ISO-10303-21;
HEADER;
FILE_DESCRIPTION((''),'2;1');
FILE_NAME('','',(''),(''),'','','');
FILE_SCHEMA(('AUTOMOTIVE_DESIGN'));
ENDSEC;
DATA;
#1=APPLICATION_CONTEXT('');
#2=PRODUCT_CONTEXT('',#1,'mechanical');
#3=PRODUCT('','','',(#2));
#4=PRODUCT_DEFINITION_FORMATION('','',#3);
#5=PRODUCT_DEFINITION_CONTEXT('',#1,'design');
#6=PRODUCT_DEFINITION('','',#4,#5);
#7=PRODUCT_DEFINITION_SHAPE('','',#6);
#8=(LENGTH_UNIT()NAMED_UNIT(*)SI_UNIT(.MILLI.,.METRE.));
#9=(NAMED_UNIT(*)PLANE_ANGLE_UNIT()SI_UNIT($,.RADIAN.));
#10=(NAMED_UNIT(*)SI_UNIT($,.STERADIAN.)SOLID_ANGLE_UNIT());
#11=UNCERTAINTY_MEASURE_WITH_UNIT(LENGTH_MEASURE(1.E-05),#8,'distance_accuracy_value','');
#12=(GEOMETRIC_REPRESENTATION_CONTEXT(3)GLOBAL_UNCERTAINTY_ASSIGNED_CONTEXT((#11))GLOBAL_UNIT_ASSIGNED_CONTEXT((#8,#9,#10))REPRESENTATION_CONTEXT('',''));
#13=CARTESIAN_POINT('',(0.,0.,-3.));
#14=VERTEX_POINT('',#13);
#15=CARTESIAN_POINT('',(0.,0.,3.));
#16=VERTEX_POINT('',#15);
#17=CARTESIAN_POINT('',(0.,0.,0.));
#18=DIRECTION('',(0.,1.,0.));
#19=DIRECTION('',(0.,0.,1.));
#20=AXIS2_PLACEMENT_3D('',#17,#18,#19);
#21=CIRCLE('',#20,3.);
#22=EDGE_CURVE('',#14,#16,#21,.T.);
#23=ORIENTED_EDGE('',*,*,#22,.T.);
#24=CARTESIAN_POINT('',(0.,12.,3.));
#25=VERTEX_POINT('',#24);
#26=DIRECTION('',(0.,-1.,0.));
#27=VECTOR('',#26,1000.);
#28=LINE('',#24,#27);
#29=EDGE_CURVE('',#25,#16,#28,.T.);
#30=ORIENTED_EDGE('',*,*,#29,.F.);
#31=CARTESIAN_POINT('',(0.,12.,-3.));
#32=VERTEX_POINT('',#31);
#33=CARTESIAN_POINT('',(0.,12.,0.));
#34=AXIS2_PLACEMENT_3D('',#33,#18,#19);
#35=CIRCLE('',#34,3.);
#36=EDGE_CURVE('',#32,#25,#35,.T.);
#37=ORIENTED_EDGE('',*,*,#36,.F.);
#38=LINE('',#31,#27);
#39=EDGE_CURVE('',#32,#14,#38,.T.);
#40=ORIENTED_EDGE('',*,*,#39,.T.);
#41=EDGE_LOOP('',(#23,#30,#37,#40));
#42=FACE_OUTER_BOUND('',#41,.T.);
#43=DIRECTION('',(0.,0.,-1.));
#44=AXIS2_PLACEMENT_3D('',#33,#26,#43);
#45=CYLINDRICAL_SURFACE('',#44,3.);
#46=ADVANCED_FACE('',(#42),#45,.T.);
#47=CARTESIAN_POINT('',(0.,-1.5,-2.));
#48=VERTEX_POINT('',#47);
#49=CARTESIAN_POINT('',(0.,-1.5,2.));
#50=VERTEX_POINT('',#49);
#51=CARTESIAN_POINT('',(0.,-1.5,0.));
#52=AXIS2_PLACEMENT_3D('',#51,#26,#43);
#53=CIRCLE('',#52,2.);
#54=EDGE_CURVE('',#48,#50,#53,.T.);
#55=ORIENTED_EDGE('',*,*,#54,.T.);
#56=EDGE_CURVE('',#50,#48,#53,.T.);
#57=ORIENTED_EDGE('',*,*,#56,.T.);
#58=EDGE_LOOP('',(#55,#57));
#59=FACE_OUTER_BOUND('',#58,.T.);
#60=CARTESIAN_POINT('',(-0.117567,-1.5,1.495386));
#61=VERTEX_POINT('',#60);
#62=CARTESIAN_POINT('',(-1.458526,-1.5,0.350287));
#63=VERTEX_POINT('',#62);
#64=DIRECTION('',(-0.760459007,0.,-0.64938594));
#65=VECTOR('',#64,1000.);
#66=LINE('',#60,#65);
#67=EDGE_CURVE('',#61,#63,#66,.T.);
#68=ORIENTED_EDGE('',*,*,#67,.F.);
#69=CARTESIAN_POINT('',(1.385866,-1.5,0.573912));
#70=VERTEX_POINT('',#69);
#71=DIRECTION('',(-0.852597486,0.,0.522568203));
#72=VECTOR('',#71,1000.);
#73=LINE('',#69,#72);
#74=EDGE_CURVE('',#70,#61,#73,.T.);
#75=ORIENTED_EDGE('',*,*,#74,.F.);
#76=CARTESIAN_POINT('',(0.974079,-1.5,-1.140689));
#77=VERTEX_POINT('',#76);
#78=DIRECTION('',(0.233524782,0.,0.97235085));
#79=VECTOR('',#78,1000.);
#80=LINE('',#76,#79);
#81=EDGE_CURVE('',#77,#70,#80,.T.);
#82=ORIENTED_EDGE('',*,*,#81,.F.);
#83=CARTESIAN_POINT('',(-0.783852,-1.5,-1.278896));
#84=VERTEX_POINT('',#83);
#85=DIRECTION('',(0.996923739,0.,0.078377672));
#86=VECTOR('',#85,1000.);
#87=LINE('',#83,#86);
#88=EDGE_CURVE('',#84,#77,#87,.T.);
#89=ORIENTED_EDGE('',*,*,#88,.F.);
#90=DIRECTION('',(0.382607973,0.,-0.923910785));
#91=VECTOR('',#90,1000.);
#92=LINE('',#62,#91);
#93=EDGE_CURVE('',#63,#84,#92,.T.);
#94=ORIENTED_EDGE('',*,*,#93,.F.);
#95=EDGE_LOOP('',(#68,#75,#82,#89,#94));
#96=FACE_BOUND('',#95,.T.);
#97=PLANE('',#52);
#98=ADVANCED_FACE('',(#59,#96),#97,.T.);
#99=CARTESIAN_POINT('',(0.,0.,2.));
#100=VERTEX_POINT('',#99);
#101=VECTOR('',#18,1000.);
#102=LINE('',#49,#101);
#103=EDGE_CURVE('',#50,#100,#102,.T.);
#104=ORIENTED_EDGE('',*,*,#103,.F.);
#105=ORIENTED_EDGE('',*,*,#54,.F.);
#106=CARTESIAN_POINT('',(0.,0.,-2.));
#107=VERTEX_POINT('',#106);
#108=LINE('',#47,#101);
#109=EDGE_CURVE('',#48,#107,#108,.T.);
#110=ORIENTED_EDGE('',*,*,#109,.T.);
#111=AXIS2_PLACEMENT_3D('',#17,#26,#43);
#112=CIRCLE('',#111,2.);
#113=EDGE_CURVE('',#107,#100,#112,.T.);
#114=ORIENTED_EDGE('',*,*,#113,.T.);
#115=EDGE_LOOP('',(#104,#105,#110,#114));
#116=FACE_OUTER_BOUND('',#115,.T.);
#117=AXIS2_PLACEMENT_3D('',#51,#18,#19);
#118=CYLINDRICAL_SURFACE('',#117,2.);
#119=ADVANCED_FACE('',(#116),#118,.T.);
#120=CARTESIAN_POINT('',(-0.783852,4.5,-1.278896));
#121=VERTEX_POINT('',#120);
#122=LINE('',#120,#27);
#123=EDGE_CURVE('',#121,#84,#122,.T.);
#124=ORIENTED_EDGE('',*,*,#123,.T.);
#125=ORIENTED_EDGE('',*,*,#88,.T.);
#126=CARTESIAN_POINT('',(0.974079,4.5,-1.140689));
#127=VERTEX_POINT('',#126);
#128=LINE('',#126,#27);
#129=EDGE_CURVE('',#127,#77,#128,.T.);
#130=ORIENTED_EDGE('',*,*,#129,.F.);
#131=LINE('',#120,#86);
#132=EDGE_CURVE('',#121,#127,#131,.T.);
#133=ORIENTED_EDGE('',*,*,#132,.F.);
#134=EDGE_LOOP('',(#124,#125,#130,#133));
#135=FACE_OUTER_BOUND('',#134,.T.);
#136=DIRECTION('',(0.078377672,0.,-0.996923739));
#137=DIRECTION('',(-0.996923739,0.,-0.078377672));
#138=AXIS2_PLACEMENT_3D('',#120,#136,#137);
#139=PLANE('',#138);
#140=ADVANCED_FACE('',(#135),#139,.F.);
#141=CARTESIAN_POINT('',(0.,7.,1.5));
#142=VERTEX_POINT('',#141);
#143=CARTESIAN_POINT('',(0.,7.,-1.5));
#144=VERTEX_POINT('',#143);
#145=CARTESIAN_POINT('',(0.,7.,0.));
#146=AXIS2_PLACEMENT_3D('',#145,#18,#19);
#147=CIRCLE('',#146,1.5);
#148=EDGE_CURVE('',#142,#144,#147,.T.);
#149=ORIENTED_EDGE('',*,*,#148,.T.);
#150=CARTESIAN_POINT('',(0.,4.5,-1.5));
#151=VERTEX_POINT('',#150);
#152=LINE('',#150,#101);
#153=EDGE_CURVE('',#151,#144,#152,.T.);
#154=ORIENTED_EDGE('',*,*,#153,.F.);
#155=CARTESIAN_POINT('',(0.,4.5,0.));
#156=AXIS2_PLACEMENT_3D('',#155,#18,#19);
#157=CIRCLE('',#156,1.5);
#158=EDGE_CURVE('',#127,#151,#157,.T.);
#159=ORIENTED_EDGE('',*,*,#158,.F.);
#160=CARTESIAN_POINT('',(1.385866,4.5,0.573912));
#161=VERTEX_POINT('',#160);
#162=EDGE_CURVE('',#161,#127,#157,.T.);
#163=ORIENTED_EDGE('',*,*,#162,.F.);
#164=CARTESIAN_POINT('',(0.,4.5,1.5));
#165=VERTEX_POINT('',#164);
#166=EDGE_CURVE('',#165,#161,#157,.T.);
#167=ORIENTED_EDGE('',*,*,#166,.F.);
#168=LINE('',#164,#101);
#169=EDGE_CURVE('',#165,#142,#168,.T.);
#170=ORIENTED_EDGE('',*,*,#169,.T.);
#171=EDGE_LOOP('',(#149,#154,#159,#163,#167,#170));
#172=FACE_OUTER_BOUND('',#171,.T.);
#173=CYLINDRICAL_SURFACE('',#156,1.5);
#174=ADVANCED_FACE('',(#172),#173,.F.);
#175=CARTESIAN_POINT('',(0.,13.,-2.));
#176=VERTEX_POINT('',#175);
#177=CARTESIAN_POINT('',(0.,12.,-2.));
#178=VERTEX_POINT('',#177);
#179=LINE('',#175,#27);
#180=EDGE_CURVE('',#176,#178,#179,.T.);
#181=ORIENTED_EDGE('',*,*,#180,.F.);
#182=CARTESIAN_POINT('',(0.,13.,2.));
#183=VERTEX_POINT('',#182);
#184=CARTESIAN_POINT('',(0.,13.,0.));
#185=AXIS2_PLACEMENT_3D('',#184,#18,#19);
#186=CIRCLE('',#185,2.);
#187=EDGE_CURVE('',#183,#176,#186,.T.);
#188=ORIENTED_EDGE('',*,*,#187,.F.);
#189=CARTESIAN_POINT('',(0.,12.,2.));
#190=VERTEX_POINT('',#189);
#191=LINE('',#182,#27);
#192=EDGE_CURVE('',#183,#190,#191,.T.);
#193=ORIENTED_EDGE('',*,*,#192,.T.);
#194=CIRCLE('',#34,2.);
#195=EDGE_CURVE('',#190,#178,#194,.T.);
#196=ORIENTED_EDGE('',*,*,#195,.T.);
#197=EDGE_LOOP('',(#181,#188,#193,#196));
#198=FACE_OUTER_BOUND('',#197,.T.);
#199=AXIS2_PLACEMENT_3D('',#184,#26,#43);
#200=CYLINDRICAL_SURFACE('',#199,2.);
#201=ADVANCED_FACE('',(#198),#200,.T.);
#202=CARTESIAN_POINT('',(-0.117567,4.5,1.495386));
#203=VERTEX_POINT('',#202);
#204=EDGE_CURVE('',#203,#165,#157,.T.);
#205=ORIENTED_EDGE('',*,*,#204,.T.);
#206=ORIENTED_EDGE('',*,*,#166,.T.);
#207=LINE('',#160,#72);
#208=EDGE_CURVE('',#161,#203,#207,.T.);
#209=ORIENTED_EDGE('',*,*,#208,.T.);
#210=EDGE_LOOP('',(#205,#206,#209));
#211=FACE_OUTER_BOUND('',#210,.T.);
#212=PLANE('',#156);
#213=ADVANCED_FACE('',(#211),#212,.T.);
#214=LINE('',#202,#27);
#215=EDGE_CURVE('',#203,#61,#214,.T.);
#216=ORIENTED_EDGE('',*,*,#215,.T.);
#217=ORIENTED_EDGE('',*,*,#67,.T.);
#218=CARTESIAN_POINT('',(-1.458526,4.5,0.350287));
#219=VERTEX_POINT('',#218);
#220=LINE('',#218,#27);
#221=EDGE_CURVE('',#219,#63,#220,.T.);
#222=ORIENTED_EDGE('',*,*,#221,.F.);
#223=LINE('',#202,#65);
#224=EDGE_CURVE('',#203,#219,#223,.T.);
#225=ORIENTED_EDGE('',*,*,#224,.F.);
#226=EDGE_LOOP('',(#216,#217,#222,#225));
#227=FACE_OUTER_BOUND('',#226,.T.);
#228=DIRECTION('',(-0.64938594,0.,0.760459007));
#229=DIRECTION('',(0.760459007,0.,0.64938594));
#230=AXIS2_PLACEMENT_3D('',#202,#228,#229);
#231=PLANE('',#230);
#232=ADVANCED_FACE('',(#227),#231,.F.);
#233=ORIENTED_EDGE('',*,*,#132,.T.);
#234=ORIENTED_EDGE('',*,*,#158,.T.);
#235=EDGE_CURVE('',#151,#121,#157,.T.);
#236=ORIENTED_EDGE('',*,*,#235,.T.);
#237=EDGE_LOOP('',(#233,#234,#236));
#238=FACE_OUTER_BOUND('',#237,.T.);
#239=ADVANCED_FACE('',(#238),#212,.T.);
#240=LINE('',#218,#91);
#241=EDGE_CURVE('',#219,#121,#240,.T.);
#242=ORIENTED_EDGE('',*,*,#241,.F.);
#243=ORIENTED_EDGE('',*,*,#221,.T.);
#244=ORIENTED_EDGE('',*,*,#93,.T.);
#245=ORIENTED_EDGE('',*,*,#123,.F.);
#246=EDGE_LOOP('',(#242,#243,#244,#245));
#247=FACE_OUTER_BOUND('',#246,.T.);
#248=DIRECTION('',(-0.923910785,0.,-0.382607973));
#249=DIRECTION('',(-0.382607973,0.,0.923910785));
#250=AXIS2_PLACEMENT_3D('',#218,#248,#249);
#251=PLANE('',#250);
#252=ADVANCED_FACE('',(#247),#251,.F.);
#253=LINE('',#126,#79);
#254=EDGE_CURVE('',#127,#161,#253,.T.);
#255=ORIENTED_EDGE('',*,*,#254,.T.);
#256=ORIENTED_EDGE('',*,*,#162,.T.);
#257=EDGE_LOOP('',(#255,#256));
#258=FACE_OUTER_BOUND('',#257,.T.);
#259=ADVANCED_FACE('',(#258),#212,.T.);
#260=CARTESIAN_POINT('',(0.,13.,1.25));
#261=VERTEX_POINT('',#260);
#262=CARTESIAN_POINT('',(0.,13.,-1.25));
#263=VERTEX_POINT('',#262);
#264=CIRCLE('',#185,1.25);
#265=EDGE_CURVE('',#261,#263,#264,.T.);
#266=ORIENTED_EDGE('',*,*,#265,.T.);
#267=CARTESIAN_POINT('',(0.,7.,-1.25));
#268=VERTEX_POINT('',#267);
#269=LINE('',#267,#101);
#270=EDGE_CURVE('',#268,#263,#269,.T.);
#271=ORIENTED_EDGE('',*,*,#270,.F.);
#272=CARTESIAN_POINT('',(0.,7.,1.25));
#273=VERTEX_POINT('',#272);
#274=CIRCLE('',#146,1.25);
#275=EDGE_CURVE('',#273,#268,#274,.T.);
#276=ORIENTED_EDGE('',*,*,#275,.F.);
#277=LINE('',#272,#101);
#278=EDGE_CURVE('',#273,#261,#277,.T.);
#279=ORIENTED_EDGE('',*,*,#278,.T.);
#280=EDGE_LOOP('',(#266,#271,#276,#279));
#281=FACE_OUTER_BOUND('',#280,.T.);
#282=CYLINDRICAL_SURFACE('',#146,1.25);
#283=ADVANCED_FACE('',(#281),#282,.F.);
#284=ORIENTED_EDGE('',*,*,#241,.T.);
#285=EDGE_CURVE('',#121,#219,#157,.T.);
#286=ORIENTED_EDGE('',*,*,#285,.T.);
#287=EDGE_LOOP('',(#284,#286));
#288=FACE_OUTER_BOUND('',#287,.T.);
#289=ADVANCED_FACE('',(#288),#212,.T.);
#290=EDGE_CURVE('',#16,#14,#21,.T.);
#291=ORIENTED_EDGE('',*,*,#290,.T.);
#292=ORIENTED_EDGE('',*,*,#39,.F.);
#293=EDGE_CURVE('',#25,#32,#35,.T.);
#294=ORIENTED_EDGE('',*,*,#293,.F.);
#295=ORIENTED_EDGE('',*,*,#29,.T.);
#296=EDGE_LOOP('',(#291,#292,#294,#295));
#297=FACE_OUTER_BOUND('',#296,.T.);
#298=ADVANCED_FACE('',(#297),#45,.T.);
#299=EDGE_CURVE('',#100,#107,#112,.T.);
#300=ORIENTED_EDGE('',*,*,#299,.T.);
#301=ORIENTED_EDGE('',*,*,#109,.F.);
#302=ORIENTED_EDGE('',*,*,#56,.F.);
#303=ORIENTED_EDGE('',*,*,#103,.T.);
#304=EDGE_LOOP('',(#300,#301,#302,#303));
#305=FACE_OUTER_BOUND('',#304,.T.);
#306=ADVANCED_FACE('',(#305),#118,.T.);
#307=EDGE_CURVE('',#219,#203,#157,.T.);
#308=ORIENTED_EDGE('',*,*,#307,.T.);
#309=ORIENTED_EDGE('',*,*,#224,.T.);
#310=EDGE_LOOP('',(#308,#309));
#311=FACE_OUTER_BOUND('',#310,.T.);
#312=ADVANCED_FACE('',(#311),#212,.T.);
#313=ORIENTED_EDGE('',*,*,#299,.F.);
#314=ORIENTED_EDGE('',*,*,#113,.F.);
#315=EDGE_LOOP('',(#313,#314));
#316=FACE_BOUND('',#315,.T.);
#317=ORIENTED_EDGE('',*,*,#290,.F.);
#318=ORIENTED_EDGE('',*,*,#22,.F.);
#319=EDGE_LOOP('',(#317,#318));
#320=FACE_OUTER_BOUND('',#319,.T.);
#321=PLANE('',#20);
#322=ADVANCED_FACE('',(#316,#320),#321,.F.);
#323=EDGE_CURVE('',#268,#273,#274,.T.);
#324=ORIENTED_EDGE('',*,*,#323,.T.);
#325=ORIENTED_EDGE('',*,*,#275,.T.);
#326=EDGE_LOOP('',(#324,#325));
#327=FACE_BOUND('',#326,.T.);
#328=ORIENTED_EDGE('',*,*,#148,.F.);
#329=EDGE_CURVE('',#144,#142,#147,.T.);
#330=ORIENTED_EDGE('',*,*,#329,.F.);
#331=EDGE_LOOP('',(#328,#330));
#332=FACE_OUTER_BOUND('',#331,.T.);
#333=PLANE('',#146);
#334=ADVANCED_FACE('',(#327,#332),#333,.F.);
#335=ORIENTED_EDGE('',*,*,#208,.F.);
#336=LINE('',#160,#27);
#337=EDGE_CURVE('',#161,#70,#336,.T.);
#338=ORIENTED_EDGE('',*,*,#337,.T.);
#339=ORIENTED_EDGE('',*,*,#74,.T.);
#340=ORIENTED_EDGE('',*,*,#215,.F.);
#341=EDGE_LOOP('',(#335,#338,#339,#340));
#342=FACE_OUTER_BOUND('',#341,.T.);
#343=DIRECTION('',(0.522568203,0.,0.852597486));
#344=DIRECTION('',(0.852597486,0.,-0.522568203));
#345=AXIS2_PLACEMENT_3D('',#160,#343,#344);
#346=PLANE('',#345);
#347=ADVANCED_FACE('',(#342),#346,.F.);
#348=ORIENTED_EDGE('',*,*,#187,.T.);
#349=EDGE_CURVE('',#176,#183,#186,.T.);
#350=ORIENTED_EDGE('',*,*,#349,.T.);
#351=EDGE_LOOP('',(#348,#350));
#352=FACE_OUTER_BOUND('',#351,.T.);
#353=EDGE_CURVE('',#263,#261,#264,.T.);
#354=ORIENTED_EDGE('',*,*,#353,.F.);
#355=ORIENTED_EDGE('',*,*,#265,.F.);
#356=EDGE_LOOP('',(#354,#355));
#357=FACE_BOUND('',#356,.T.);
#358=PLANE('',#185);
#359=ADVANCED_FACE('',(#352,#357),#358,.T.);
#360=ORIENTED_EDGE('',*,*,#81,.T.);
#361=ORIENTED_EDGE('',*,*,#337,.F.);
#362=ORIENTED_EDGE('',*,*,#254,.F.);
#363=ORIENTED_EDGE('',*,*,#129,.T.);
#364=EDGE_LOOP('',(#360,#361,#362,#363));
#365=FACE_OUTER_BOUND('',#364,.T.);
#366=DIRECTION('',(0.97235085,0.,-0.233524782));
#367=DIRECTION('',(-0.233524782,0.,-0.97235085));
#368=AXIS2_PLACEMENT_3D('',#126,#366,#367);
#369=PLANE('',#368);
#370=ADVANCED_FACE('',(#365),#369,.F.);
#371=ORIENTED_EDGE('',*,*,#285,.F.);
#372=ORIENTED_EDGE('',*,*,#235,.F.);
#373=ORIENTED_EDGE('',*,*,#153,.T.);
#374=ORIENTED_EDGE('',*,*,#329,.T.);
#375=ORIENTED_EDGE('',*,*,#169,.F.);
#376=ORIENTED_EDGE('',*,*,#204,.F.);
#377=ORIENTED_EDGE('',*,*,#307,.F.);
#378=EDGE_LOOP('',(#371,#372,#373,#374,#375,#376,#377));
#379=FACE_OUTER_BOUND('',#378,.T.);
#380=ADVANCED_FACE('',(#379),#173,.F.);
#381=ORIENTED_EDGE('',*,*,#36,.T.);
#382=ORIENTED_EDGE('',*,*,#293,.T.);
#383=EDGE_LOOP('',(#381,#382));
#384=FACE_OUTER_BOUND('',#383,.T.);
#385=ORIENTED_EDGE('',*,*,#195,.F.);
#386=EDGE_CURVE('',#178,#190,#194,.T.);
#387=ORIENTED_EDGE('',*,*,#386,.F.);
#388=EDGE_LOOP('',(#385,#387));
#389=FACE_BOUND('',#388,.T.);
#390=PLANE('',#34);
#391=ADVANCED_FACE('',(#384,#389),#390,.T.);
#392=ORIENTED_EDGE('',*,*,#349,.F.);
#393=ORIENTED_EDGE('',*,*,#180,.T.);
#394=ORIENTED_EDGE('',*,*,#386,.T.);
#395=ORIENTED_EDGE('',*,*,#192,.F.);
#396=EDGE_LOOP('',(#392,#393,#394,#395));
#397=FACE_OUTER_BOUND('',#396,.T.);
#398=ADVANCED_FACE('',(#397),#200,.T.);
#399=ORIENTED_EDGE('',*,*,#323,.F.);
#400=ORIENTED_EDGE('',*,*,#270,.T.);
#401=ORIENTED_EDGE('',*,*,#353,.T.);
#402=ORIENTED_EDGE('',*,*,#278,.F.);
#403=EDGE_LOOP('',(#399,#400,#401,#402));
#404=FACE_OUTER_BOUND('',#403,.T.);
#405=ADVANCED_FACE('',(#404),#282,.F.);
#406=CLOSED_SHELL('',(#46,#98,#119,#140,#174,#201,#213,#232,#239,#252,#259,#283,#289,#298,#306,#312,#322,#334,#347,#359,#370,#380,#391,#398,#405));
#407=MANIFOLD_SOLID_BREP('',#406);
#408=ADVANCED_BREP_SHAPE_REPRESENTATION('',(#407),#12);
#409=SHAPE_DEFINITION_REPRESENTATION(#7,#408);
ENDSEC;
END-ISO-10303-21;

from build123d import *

# Parameters (mm, degrees)
SKETCH_2_R           = 3
BOSS_EXTRUDE_1_DEPTH = 12
SKETCH_3_R           = 2
BOSS_EXTRUDE_2_DEPTH = 1
BOSS_EXTRUDE_START   = 1.5
SKETCH_4_R           = 2
BOSS_EXTRUDE_3_DEPTH = 1.5
SKETCH_5_R           = 1.25
CUT_EXTRUDE_1_DEPTH  = 6
SKETCH_6_R           = 1.5
CUT_EXTRUDE_2_DEPTH  = 2.5
CUT_EXTRUDE_3_DEPTH  = 6


with BuildPart() as part:
    # Sketch 2 → Boss-Extrude 1 (new body)
    with BuildSketch(Plane(origin=(0, 0, 0), x_dir=(1, 0, 0), z_dir=(0, 1, 0))):
        with Locations(Location((0, 0, 0), (0, 0, 270))):
            Circle(SKETCH_2_R)
    extrude(amount=BOSS_EXTRUDE_1_DEPTH)

    # Sketch 3 → Boss-Extrude 2 (add)
    with BuildSketch(Plane(origin=(0, 12, 0), x_dir=(1, 0, 0), z_dir=(0, 1, 0))):
        with Locations(Location((0, 0, 0), (0, 0, 270))):
            Circle(SKETCH_3_R)
    extrude(amount=BOSS_EXTRUDE_2_DEPTH)

    # Sketch 4 → Boss-Extrude 3 (add)
    with BuildSketch(Plane(origin=(0, 0, 0), x_dir=(-1, 0, 0), z_dir=(0, -1, 0)).offset(BOSS_EXTRUDE_START)):
        with Locations(Location((0, 0, 0), (0, 0, 270))):
            Circle(SKETCH_4_R)
    extrude(amount=-BOSS_EXTRUDE_3_DEPTH)

    # Sketch 5 → Cut-Extrude 1 (cut)
    with BuildSketch(Plane(origin=(0, 13, 0), x_dir=(1, 0, 0), z_dir=(0, 1, 0))):
        with Locations(Location((0, 0, 0), (0, 0, 270))):
            Circle(SKETCH_5_R)
    extrude(amount=-CUT_EXTRUDE_1_DEPTH, mode=Mode.SUBTRACT)

    # Sketch 6 → Cut-Extrude 2 (cut)
    with BuildSketch(Plane(origin=(0, 7, 0), x_dir=(1, 0, 0), z_dir=(0, 1, 0))):
        with Locations(Location((0, 0, 0), (0, 0, 270))):
            Circle(SKETCH_6_R)
    extrude(amount=-CUT_EXTRUDE_2_DEPTH, mode=Mode.SUBTRACT)

    # Sketch 7 → Cut-Extrude 3 (cut)
    with BuildSketch(Plane(origin=(0, -1.5, 0), x_dir=(-1, 0, 0), z_dir=(0, -1, 0))):
        Polygon((-0.97407891, 1.14068851), (-1.385866178, -0.57391196), (0.117566508, -1.495385608), (1.458526276, -0.350287172), (0.783852304, 1.27889623), align=None)
    extrude(amount=-CUT_EXTRUDE_3_DEPTH, mode=Mode.SUBTRACT)


solid = part.part
